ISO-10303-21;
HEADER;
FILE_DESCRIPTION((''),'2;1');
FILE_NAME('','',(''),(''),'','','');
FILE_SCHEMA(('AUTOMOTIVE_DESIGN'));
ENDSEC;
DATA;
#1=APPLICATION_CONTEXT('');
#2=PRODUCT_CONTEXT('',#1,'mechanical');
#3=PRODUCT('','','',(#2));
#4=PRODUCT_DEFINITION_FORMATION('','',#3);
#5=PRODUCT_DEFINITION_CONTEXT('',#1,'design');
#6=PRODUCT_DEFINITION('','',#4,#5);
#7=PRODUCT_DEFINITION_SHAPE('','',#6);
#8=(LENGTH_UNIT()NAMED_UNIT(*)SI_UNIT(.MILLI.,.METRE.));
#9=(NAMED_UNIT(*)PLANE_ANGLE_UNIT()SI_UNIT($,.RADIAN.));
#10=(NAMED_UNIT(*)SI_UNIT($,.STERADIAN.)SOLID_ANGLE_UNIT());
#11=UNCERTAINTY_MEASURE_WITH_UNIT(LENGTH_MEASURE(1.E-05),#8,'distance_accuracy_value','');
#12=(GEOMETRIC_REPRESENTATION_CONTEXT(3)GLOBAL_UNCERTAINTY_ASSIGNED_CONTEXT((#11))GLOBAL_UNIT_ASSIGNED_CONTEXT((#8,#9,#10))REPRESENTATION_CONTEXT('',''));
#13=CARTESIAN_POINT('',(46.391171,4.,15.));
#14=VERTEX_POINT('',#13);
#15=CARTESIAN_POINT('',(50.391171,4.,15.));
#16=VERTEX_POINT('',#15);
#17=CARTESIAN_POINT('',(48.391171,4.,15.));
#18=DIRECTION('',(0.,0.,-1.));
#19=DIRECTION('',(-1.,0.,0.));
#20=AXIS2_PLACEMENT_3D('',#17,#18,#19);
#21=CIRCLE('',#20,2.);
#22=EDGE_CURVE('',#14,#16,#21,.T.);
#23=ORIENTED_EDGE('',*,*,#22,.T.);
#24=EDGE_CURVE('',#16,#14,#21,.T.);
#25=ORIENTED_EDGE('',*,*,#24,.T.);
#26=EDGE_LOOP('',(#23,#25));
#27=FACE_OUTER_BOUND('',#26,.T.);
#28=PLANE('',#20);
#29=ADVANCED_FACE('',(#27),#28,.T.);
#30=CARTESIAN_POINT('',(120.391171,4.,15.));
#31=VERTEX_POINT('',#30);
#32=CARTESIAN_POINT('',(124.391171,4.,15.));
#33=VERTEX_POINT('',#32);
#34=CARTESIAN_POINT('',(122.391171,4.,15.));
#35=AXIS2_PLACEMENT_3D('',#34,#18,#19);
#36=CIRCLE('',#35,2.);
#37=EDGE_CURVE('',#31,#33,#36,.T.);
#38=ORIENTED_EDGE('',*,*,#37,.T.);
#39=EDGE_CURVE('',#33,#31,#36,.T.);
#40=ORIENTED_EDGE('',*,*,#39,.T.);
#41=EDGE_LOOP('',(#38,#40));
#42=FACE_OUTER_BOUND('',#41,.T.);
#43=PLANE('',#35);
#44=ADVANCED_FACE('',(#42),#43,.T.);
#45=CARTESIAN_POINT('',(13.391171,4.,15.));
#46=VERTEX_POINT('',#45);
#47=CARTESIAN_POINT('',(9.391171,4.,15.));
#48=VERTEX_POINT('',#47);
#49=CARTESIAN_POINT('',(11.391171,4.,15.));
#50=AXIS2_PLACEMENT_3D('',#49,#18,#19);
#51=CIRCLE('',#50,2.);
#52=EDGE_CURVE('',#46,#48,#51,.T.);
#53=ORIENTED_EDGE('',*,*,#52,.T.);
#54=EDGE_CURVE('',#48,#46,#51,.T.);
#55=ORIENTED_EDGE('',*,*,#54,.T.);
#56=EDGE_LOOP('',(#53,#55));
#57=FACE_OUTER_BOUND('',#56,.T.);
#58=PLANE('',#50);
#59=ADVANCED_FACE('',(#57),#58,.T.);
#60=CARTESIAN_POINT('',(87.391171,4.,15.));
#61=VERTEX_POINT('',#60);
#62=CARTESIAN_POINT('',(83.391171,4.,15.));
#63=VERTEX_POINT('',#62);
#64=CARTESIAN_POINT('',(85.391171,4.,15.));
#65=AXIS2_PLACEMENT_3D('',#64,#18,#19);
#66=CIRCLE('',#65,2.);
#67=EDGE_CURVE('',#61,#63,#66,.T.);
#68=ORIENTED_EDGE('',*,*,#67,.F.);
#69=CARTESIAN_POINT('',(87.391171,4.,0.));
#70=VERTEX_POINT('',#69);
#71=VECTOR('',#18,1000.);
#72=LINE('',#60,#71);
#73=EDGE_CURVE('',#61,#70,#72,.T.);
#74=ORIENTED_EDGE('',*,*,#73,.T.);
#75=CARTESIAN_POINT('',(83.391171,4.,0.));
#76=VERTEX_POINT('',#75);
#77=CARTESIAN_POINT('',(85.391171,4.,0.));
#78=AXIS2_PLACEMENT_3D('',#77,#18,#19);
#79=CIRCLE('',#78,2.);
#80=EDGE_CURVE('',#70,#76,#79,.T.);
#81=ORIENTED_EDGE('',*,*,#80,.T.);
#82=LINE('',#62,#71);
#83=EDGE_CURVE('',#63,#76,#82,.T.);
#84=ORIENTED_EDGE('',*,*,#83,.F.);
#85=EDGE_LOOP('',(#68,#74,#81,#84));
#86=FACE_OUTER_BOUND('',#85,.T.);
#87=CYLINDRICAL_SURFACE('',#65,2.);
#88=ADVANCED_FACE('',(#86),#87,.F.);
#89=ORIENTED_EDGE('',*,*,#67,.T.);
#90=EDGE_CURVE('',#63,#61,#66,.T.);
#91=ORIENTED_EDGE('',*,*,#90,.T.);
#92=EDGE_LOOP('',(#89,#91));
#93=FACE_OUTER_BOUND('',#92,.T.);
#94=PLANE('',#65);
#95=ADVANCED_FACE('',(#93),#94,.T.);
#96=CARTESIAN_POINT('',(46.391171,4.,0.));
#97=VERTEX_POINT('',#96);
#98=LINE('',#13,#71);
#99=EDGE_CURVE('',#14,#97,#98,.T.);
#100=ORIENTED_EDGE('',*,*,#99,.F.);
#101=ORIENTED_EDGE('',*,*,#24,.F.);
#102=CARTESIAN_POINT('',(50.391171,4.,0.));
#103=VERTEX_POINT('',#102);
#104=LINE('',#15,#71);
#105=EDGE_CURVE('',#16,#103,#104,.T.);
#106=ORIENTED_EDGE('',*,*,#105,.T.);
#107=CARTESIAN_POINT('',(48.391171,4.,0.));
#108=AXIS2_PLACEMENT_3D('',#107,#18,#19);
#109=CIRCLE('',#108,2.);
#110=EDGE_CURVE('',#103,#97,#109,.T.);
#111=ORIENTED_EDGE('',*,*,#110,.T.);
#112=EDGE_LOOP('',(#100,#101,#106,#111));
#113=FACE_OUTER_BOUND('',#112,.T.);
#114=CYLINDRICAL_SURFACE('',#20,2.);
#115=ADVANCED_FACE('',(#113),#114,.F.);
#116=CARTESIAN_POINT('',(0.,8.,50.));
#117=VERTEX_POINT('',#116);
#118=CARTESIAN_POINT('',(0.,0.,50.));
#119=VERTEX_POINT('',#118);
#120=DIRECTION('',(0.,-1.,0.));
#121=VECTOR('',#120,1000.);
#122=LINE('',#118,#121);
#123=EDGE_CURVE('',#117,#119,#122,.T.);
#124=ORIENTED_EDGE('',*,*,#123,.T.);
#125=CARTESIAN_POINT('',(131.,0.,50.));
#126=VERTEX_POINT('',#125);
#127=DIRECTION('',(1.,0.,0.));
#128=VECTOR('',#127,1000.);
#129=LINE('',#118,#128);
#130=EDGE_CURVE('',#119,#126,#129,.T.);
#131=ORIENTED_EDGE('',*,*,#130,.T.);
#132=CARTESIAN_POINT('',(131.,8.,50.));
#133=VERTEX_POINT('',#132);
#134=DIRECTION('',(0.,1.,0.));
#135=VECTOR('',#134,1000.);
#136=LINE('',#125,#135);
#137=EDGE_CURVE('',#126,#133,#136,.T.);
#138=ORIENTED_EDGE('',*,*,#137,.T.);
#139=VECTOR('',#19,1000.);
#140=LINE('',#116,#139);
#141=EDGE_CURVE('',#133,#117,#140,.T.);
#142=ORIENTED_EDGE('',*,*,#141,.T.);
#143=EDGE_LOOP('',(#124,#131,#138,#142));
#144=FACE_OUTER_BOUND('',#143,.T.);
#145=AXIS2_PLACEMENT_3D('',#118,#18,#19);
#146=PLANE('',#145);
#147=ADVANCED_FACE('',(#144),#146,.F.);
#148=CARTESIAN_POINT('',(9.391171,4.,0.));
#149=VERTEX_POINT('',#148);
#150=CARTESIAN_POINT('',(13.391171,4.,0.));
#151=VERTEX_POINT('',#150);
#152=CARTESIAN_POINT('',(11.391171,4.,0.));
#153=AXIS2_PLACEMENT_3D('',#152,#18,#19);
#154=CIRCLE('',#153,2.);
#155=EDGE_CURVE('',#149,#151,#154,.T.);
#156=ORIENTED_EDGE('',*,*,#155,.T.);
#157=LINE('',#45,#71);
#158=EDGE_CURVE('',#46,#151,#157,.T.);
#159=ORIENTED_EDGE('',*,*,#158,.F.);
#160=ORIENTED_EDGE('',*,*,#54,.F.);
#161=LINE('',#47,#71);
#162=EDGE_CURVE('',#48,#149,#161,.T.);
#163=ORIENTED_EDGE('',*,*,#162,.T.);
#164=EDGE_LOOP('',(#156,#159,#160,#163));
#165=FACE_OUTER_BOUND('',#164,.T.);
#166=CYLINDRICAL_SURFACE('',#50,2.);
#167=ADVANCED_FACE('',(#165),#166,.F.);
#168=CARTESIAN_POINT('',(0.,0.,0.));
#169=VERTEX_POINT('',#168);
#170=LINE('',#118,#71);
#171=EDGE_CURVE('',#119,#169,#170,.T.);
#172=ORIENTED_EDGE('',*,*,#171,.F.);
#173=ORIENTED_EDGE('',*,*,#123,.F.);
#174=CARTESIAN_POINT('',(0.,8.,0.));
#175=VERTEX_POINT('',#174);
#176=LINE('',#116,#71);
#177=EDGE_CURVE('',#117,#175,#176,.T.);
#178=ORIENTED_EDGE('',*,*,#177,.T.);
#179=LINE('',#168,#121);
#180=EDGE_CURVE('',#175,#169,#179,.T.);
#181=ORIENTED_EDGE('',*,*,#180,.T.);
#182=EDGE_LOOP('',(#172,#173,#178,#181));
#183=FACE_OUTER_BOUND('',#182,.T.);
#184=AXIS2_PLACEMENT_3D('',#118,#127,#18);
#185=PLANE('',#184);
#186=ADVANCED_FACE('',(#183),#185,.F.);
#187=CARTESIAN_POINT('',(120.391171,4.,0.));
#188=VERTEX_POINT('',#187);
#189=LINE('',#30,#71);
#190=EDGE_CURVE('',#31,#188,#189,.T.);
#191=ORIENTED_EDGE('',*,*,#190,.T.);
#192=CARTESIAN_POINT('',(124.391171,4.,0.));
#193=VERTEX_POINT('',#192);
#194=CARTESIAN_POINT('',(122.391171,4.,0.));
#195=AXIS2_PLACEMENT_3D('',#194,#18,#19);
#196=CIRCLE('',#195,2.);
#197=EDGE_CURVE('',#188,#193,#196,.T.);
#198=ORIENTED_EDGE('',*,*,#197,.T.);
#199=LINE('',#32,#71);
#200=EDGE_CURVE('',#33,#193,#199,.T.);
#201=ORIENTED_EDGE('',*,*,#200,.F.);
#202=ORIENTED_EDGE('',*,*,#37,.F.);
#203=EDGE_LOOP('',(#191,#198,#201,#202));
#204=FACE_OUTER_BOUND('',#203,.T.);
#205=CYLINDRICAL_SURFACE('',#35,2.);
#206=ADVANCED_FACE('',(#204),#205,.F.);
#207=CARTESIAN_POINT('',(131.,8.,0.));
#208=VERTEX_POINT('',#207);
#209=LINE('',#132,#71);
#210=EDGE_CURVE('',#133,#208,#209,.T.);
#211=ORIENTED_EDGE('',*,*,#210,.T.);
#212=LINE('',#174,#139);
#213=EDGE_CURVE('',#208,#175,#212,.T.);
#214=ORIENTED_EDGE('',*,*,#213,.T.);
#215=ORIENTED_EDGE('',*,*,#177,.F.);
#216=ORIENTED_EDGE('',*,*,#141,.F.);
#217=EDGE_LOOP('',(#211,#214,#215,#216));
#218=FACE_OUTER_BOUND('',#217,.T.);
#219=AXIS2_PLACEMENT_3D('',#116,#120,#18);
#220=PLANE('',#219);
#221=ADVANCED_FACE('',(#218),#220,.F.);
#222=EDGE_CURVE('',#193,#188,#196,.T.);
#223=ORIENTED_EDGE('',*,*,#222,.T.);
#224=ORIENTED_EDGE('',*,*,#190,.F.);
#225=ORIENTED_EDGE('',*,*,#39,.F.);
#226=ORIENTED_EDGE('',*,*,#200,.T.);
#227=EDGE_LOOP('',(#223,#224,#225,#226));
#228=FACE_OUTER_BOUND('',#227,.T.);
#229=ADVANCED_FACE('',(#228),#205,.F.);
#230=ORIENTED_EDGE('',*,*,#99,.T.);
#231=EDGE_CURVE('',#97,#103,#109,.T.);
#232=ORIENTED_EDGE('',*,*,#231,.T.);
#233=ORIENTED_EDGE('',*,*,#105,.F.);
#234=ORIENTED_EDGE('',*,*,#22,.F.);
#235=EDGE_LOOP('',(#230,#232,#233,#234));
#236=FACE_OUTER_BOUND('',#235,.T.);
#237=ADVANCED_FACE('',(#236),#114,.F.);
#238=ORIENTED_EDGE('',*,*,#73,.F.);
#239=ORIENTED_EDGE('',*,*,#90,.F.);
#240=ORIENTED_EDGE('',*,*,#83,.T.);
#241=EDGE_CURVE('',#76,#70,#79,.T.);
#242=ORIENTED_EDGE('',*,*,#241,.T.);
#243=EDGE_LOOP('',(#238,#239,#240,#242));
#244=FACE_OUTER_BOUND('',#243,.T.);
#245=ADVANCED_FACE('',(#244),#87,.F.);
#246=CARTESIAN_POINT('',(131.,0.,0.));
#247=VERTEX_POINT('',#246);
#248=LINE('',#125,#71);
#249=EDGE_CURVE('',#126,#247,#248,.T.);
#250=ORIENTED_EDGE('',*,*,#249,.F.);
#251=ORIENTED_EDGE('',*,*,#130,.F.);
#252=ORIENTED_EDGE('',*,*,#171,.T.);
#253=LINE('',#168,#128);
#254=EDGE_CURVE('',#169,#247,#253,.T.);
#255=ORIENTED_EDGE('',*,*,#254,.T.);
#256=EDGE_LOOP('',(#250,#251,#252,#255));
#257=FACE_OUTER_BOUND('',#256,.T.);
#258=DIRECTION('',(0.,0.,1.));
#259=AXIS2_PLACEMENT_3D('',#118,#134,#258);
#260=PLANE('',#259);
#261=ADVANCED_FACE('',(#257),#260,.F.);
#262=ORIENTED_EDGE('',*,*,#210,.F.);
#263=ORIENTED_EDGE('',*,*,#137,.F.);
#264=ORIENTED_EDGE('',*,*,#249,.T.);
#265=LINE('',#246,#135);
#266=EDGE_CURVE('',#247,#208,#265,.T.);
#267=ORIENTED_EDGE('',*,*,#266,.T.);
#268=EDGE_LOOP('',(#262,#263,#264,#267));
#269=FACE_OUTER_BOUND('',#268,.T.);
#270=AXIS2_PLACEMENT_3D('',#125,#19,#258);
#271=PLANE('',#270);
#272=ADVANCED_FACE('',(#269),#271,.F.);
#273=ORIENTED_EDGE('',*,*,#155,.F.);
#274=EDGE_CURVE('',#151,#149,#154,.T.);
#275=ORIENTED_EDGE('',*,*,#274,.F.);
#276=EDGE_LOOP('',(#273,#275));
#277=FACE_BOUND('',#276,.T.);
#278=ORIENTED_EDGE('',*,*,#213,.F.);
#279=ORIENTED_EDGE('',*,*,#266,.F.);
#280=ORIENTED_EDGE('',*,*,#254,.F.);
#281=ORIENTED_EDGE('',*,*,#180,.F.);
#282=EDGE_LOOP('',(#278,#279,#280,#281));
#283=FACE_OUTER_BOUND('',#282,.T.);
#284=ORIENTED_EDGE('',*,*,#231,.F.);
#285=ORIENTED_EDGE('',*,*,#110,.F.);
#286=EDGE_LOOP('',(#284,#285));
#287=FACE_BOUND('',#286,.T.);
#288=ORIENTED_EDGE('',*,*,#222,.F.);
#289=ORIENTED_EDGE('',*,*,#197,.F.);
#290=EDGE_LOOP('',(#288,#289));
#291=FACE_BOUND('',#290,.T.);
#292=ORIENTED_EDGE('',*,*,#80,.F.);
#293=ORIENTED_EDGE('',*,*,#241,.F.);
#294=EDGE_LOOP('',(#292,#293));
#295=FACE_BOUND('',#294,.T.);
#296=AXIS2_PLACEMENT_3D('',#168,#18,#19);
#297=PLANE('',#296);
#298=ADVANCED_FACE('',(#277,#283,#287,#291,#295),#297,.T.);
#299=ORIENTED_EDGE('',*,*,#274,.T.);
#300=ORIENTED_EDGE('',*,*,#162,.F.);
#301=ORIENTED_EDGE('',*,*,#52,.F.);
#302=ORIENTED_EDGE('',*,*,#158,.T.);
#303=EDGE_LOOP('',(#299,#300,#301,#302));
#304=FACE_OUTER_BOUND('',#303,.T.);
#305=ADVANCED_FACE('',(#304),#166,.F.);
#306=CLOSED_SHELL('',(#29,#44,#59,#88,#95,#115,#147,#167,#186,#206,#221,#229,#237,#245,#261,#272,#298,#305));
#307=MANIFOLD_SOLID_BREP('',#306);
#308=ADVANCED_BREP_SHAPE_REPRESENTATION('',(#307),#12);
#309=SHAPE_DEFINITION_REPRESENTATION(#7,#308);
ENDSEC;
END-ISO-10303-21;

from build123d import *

# Parameters (mm, degrees)
SKETCH1_W           = 131
SKETCH1_H           = 8
BOSS_EXTRUDE1_DEPTH = 50
SKETCH2_R           = 2
CUT_EXTRUDE1_DEPTH  = 15


with BuildPart() as part:
    # Sketch1 → Boss-Extrude1 (new body)
    with BuildSketch(Plane.XY):
        with Locations((65.5, 4)):
            Rectangle(SKETCH1_W, SKETCH1_H)
    extrude(amount=BOSS_EXTRUDE1_DEPTH)

    # Sketch2 → Cut-Extrude1 (cut)
    with BuildSketch(Plane(origin=(0, 0, 0), x_dir=(-1, 0, 0), z_dir=(0, 0, -1))):
        with Locations((-122.391171487, 4)):
            Circle(SKETCH2_R)
        with Locations((-85.391171487, 4)):
            Circle(SKETCH2_R)
        with Locations((-48.391171487, 4)):
            Circle(SKETCH2_R)
        with Locations((-11.391171487, 4)):
            Circle(SKETCH2_R)
    extrude(amount=-CUT_EXTRUDE1_DEPTH, mode=Mode.SUBTRACT)


solid = part.part
